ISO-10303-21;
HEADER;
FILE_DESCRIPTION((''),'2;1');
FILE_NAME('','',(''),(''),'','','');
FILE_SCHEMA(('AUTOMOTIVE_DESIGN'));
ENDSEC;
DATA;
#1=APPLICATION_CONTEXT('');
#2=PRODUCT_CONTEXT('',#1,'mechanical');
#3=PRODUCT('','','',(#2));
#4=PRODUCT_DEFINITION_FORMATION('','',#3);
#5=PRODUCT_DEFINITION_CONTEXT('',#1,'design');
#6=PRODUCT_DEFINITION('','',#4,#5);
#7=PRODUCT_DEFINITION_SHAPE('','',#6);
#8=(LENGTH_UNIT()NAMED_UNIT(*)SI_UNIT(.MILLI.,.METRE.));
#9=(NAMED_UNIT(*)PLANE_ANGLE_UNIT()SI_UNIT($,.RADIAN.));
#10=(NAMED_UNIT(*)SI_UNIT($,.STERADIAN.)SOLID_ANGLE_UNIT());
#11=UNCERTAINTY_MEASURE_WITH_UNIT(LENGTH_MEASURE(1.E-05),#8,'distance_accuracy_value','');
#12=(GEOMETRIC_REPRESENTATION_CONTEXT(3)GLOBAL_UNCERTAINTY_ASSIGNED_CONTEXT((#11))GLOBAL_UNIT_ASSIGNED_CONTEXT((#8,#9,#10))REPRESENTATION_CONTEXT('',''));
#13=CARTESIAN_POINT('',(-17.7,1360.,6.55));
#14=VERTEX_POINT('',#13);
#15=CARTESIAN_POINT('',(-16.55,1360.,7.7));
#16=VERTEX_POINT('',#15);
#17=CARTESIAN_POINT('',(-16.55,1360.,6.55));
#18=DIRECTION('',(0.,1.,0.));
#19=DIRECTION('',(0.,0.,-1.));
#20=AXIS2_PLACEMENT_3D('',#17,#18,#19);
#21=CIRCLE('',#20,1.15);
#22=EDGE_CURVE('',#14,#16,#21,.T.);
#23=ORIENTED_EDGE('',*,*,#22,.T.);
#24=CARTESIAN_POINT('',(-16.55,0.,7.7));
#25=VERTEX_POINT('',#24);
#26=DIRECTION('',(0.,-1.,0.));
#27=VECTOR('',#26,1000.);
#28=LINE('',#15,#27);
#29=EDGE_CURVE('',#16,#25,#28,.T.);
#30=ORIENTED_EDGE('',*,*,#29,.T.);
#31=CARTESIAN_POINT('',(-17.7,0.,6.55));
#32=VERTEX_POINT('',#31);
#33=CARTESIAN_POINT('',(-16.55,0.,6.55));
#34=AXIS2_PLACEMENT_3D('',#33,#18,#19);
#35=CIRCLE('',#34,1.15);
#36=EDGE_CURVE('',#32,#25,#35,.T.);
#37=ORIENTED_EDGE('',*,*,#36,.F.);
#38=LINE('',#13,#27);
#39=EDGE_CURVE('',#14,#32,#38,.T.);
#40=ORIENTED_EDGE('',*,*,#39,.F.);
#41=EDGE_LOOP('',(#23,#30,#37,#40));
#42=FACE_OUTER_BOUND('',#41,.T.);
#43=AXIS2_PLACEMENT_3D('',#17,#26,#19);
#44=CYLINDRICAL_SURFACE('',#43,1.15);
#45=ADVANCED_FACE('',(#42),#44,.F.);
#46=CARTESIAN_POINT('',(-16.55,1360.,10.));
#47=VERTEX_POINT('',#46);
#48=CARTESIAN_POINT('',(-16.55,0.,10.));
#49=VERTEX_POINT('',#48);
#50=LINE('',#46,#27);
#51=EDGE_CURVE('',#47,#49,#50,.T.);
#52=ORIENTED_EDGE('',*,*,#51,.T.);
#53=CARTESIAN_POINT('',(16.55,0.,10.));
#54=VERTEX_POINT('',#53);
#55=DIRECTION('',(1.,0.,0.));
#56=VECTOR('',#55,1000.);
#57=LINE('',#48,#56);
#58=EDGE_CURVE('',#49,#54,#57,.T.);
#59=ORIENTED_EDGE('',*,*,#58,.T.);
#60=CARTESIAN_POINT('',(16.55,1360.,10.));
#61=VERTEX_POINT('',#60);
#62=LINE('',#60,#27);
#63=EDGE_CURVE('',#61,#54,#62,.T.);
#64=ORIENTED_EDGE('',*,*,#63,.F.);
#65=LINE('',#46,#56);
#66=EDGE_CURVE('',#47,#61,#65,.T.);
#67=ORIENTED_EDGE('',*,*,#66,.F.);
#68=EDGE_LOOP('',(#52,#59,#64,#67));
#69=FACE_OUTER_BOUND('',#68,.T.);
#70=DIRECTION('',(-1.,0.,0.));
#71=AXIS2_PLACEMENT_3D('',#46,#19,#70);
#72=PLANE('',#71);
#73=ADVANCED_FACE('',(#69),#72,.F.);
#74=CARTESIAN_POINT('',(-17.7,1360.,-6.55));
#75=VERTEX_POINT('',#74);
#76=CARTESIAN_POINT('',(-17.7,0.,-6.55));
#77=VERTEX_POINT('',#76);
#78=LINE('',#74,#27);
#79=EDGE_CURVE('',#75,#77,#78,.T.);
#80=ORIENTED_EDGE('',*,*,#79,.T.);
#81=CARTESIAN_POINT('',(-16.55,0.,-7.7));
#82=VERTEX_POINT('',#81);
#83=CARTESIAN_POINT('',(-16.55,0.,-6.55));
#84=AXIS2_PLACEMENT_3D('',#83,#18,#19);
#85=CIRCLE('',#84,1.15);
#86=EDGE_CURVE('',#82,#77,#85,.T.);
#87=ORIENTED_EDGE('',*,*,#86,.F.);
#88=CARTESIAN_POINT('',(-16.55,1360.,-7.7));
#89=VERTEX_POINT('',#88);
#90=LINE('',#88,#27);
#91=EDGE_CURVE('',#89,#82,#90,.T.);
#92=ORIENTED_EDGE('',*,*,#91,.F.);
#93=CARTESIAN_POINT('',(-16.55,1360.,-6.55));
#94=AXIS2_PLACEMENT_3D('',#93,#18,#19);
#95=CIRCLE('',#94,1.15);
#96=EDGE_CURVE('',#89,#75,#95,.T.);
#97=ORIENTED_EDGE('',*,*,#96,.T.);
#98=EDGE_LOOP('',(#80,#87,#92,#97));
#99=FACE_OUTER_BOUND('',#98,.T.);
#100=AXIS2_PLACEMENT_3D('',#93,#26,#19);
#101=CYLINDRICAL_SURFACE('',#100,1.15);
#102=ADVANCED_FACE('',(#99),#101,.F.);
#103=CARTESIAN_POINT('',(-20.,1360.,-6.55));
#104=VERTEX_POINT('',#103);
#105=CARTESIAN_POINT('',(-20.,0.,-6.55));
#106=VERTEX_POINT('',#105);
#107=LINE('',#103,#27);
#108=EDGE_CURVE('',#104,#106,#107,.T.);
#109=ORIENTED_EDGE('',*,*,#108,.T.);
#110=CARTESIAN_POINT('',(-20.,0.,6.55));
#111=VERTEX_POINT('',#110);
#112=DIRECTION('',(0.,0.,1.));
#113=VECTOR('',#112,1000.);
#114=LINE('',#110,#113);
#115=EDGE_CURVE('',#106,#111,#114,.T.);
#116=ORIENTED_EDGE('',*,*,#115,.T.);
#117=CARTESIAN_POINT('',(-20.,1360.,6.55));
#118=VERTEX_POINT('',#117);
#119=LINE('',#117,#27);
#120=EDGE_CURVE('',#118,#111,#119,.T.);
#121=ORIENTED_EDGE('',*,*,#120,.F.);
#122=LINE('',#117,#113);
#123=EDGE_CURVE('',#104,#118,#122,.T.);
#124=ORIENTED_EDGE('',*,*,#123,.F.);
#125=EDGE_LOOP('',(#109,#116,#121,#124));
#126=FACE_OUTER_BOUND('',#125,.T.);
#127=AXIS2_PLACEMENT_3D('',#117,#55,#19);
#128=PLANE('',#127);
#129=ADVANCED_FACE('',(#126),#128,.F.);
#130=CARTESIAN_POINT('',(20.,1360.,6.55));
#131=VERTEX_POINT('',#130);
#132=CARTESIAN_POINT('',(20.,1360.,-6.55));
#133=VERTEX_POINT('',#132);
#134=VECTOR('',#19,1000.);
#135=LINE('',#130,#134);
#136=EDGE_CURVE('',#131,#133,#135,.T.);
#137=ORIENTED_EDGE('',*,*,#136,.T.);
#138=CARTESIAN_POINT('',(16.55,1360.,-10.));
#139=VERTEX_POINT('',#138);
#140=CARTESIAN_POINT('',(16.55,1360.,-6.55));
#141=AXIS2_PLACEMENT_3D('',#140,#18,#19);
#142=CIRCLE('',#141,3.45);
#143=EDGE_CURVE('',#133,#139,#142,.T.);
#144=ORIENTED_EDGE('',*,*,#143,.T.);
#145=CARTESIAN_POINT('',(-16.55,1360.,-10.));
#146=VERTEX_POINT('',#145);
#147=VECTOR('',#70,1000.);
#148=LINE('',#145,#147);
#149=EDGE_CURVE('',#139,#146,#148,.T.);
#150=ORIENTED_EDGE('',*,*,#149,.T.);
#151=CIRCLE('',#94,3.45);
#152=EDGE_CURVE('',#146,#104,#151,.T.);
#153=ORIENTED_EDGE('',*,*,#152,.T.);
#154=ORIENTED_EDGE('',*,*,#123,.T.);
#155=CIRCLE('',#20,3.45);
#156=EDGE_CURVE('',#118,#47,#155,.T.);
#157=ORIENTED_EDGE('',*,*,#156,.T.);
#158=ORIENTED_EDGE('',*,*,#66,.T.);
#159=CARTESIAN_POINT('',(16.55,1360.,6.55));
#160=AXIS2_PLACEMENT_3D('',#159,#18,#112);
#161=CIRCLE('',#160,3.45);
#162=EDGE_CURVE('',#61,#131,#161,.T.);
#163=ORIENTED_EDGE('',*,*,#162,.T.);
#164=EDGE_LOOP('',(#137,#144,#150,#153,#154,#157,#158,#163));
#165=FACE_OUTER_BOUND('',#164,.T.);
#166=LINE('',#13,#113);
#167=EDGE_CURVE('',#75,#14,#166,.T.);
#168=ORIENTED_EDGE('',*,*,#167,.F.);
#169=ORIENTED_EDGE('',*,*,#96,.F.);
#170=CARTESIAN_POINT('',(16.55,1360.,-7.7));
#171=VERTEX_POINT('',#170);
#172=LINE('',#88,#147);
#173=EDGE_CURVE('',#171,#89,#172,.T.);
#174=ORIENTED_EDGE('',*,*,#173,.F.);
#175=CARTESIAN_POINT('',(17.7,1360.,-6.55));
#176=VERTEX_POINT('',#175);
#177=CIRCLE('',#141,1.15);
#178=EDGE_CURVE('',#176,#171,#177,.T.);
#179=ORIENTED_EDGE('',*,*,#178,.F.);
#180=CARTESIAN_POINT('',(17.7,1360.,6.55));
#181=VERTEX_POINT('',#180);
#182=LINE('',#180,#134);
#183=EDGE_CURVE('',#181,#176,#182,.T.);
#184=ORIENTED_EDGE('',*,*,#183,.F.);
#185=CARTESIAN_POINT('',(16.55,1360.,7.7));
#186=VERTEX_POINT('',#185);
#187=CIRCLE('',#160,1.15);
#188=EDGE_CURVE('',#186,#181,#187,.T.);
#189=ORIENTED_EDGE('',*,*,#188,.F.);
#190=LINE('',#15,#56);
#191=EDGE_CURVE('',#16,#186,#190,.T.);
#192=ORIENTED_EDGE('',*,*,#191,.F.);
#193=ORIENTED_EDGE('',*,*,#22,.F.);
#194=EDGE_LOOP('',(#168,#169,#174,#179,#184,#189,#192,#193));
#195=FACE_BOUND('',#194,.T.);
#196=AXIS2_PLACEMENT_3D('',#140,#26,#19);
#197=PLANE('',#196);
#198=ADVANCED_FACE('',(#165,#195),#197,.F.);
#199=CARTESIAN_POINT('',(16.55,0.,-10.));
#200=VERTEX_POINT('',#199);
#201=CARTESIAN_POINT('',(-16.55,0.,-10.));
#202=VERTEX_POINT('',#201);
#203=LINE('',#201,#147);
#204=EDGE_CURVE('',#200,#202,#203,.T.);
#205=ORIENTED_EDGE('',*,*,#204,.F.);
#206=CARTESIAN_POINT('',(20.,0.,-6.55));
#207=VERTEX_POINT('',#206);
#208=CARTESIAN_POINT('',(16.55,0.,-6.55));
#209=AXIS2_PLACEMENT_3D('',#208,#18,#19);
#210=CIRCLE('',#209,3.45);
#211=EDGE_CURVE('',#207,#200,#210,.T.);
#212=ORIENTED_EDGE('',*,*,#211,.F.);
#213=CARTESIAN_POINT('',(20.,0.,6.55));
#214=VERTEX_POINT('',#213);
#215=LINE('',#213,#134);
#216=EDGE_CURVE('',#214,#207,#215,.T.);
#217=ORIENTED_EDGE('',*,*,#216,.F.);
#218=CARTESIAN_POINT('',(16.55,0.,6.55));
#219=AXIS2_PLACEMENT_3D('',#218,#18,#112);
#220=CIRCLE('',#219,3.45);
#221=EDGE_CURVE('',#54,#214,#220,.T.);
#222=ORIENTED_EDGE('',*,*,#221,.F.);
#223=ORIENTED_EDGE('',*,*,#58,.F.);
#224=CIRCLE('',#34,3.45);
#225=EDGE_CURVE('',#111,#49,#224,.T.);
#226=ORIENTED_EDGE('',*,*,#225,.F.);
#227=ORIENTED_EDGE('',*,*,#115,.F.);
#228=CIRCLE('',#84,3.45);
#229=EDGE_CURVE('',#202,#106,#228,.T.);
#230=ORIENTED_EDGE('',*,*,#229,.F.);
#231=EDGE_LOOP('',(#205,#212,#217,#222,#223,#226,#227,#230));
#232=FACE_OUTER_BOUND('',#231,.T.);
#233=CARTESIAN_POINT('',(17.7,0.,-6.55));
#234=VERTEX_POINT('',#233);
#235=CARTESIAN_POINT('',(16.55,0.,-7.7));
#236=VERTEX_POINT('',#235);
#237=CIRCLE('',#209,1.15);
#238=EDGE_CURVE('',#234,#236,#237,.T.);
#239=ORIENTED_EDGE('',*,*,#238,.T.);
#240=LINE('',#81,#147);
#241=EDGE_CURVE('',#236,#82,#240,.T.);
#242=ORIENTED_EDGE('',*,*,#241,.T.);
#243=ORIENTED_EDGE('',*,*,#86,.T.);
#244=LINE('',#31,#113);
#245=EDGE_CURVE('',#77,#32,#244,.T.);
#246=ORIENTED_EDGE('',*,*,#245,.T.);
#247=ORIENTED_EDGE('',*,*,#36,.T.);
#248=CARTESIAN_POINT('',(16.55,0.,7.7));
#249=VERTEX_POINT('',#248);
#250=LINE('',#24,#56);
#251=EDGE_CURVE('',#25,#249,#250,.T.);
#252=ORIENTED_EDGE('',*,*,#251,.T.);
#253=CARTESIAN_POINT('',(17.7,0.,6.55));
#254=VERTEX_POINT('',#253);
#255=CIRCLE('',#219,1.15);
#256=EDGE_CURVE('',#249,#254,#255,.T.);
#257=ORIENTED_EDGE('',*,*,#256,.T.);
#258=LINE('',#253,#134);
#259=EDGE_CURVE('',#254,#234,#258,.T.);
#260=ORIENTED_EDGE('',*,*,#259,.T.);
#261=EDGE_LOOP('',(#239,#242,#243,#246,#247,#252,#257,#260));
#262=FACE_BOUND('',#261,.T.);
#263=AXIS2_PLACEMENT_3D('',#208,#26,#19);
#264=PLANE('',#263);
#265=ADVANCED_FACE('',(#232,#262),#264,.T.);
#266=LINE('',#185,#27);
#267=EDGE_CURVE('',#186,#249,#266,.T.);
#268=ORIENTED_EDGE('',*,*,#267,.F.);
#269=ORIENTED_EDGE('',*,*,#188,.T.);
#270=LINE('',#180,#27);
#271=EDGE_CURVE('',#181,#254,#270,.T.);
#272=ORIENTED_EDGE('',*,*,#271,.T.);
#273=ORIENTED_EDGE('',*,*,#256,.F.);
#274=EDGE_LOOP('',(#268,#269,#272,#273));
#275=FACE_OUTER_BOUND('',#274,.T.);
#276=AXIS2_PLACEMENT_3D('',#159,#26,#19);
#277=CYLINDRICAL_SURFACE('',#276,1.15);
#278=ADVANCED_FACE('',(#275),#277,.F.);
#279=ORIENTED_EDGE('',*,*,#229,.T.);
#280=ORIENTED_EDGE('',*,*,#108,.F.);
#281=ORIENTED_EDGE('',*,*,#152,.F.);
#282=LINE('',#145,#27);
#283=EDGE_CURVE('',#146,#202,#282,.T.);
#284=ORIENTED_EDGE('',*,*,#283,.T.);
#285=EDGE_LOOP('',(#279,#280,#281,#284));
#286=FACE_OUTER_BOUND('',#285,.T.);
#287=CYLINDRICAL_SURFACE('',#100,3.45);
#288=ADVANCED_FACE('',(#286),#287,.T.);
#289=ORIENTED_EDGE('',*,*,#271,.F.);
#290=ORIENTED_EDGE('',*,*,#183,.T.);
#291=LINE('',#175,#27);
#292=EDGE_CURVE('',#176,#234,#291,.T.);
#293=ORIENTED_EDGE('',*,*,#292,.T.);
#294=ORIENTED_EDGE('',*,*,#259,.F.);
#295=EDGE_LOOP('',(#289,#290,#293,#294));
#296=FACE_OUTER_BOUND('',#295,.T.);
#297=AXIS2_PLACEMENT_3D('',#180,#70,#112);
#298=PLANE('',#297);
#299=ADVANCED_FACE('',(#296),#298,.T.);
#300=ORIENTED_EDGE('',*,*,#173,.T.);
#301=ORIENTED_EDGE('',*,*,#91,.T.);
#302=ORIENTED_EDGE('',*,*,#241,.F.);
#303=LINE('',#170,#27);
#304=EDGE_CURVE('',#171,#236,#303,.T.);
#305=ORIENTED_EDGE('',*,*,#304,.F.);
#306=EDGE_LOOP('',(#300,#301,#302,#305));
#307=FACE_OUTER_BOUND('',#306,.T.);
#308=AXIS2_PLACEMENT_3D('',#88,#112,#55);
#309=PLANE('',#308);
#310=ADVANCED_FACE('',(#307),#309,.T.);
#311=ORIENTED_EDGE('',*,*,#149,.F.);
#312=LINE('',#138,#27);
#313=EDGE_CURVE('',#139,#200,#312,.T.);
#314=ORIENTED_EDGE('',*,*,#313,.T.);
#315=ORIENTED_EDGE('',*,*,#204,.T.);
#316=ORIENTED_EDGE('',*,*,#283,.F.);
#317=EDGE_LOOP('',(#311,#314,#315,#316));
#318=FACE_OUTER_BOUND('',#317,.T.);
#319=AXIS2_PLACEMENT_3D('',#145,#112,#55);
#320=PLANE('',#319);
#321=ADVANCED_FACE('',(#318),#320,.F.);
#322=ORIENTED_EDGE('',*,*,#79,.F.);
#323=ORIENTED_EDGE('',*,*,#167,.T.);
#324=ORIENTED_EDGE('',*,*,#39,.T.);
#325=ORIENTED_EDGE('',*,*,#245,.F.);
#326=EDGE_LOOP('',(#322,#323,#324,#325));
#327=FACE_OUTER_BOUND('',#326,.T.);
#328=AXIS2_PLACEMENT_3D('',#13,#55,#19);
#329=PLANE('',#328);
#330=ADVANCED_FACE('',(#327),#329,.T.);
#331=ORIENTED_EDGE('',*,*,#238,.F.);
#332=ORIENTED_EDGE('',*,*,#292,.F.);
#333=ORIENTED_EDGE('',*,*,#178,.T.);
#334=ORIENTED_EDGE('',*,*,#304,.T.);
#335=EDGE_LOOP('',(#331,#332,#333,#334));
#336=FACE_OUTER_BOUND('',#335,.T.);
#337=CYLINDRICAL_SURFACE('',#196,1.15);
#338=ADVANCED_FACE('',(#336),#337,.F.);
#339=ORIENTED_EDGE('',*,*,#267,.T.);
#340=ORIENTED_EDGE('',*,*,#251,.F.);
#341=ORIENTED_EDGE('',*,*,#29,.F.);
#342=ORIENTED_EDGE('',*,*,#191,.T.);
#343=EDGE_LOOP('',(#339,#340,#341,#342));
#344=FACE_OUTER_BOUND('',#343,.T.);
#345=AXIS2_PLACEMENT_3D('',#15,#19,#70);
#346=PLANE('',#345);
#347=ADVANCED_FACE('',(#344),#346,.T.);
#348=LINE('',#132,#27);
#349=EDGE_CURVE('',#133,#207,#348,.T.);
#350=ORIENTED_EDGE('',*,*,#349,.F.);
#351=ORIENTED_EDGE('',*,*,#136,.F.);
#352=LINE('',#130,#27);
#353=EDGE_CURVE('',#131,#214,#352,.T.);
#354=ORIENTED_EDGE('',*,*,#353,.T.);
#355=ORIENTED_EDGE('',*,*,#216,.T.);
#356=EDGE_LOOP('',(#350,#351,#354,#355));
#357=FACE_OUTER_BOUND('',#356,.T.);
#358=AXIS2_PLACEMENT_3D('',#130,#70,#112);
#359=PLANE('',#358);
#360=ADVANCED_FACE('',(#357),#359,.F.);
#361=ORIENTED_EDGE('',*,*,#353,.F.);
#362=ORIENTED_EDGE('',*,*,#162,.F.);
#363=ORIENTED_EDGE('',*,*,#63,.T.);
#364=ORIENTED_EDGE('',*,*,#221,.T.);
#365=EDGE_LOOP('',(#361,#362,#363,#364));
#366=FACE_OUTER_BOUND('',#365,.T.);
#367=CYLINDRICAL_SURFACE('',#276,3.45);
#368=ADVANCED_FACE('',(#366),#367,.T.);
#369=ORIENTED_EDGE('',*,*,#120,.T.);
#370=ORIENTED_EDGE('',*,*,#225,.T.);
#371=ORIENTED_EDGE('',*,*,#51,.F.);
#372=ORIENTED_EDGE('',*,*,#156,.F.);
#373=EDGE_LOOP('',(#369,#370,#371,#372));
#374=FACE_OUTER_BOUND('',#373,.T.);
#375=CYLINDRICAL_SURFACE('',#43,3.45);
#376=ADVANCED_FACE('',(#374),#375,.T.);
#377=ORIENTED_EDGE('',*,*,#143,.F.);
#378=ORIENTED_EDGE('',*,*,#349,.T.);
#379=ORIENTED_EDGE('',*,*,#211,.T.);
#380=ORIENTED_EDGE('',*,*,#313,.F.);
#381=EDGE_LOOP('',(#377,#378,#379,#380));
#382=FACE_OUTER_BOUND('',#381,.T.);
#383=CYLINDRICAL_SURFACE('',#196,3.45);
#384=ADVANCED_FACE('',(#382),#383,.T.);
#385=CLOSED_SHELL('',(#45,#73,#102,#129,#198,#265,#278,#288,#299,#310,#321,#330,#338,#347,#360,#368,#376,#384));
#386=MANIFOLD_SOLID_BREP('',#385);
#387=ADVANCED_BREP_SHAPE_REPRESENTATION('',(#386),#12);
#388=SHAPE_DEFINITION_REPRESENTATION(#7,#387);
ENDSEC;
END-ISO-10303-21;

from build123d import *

# Parameters (mm, degrees)
BOSS_EXTRUDE1_DEPTH = 1360


with BuildPart() as part:
    # Sketch1 → Boss-Extrude1 (new body)
    with BuildSketch(Plane(origin=(0, 0, 0), x_dir=(1, 0, 0), z_dir=(0, 1, 0))):
        with BuildLine():
            Line((-16.55, -10), (16.55, -10))
            ThreePointArc((16.55, -10), (18.989518395, -8.989518395), (20, -6.55))
            Line((20, -6.55), (20, 6.55))
            ThreePointArc((20, 6.55), (18.989518395, 8.989518395), (16.55, 10))
            Line((16.55, 10), (-16.55, 10))
            ThreePointArc((-16.55, 10), (-18.989518395, 8.989518395), (-20, 6.55))
            Line((-20, 6.55), (-20, -6.55))
            ThreePointArc((-20, -6.55), (-18.989518395, -8.989518395), (-16.55, -10))
        make_face()
        with BuildLine():
            Line((-16.55, -7.7), (16.55, -7.7))
            ThreePointArc((16.55, -7.7), (17.363172798, -7.363172798), (17.7, -6.55))
            Line((17.7, -6.55), (17.7, 6.55))
            ThreePointArc((17.7, 6.55), (17.363172798, 7.363172798), (16.55, 7.7))
            Line((16.55, 7.7), (-16.55, 7.7))
            ThreePointArc((-16.55, 7.7), (-17.363172798, 7.363172798), (-17.7, 6.55))
            Line((-17.7, 6.55), (-17.7, -6.55))
            ThreePointArc((-17.7, -6.55), (-17.363172798, -7.363172798), (-16.55, -7.7))
        make_face(mode=Mode.SUBTRACT)
    extrude(amount=BOSS_EXTRUDE1_DEPTH)


solid = part.part
